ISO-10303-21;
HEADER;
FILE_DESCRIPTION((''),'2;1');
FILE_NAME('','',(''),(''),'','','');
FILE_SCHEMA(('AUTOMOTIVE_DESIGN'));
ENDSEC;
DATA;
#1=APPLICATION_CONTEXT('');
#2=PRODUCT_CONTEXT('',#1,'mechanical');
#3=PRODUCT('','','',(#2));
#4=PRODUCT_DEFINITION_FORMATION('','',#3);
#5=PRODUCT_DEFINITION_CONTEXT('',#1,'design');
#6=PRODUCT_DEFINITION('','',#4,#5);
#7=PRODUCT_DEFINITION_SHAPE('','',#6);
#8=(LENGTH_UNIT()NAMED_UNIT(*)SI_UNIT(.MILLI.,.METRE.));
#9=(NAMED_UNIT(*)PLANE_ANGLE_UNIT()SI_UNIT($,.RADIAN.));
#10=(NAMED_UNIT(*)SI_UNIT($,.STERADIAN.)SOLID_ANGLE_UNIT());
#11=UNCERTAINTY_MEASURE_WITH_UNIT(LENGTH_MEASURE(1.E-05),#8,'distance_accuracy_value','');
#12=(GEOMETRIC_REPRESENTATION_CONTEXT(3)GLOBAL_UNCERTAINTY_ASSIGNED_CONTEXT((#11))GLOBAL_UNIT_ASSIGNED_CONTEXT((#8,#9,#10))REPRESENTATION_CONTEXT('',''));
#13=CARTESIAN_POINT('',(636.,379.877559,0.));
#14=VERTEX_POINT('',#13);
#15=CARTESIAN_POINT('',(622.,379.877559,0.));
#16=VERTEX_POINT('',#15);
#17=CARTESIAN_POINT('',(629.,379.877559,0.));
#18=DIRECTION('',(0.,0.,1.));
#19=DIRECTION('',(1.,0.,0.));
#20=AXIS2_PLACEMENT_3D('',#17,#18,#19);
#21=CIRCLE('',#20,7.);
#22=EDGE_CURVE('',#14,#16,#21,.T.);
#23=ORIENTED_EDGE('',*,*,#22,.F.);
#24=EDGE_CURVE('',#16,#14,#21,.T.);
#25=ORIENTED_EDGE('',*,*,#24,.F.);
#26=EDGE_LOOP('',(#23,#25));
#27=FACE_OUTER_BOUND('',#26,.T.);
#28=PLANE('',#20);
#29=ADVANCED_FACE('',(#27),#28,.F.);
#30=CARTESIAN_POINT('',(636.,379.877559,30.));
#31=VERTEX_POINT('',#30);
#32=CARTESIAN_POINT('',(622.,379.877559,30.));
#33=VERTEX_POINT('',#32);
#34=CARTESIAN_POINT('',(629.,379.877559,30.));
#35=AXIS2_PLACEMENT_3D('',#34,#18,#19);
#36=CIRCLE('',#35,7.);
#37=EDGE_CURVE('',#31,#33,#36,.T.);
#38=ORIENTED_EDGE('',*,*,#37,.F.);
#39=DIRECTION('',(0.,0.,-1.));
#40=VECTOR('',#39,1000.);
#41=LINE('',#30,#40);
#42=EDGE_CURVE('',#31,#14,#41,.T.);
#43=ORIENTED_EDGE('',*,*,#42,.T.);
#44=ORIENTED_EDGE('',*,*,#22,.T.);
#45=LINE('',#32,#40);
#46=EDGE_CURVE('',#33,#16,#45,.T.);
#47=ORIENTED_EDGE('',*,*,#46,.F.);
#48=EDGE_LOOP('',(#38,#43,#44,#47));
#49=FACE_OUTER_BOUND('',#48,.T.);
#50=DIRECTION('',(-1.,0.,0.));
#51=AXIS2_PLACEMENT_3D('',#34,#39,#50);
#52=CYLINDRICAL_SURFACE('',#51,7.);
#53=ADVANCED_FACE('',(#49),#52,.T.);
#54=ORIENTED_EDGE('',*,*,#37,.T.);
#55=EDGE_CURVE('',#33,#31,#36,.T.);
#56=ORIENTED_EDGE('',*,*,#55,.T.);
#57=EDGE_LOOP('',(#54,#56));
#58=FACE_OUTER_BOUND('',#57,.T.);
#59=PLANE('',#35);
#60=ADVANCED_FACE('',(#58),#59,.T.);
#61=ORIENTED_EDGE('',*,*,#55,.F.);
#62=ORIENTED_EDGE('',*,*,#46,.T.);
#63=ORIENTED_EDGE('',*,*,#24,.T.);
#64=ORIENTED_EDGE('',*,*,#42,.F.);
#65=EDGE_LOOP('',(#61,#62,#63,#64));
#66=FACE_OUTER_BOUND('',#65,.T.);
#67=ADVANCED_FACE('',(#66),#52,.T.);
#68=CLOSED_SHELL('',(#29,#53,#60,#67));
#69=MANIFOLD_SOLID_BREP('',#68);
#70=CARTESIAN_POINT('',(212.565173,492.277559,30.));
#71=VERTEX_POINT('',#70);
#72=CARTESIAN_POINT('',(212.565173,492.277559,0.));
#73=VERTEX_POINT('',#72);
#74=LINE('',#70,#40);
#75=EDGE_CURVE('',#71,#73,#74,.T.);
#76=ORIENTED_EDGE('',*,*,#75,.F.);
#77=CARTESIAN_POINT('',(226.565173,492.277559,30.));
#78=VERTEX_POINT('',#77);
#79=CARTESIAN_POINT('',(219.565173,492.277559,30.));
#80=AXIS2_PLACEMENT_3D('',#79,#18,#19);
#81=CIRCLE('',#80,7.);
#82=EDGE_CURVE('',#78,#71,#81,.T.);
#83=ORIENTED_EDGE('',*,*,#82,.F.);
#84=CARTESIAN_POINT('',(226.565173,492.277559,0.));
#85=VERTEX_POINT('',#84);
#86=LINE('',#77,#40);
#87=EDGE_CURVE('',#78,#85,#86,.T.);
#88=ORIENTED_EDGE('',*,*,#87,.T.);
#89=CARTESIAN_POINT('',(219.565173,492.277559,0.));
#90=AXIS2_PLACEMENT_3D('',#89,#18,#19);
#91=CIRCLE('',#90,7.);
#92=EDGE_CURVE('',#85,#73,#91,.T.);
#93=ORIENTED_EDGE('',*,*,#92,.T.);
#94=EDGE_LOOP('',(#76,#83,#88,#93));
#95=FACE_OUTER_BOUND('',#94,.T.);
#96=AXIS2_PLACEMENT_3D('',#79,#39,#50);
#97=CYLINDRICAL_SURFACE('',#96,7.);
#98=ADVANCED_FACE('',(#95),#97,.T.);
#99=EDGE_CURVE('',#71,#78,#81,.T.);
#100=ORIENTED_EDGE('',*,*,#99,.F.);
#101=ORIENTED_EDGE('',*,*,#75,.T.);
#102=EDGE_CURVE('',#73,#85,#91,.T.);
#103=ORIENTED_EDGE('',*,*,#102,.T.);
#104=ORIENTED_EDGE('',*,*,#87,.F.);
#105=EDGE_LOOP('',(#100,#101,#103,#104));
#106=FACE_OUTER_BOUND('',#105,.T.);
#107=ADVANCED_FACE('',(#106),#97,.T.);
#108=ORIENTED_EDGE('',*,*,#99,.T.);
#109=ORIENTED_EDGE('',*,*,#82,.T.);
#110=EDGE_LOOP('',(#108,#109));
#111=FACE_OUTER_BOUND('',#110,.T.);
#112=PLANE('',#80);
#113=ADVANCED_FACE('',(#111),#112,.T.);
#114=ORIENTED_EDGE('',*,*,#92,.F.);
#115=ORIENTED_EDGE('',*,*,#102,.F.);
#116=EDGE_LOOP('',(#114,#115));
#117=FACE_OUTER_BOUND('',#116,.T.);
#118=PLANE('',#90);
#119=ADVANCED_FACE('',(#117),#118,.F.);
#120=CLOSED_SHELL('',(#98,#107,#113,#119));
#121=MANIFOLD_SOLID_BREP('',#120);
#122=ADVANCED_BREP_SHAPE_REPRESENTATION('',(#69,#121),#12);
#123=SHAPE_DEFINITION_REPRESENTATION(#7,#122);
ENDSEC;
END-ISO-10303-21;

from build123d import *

# Parameters (mm, degrees)
SKETCH1_R             = 7
BOSS_EXTRUDE1_DEPTH   = 30
BOSS_EXTRUDE1_2_DEPTH = 30


with BuildPart() as part:
    # Sketch1 → Boss-Extrude1 (new body)
    with BuildSketch(Plane.XY):
        with Locations((629, 379.877558602)):
            Circle(SKETCH1_R)
    extrude(amount=BOSS_EXTRUDE1_DEPTH)


with BuildPart() as body_2:
    # Sketch1 → Boss-Extrude1 2 (new body)
    with BuildSketch(Plane.XY):
        with Locations((219.565172816, 492.277558602)):
            Circle(SKETCH1_R)
    extrude(amount=BOSS_EXTRUDE1_2_DEPTH)


solid = Compound([part.part, body_2.part])
